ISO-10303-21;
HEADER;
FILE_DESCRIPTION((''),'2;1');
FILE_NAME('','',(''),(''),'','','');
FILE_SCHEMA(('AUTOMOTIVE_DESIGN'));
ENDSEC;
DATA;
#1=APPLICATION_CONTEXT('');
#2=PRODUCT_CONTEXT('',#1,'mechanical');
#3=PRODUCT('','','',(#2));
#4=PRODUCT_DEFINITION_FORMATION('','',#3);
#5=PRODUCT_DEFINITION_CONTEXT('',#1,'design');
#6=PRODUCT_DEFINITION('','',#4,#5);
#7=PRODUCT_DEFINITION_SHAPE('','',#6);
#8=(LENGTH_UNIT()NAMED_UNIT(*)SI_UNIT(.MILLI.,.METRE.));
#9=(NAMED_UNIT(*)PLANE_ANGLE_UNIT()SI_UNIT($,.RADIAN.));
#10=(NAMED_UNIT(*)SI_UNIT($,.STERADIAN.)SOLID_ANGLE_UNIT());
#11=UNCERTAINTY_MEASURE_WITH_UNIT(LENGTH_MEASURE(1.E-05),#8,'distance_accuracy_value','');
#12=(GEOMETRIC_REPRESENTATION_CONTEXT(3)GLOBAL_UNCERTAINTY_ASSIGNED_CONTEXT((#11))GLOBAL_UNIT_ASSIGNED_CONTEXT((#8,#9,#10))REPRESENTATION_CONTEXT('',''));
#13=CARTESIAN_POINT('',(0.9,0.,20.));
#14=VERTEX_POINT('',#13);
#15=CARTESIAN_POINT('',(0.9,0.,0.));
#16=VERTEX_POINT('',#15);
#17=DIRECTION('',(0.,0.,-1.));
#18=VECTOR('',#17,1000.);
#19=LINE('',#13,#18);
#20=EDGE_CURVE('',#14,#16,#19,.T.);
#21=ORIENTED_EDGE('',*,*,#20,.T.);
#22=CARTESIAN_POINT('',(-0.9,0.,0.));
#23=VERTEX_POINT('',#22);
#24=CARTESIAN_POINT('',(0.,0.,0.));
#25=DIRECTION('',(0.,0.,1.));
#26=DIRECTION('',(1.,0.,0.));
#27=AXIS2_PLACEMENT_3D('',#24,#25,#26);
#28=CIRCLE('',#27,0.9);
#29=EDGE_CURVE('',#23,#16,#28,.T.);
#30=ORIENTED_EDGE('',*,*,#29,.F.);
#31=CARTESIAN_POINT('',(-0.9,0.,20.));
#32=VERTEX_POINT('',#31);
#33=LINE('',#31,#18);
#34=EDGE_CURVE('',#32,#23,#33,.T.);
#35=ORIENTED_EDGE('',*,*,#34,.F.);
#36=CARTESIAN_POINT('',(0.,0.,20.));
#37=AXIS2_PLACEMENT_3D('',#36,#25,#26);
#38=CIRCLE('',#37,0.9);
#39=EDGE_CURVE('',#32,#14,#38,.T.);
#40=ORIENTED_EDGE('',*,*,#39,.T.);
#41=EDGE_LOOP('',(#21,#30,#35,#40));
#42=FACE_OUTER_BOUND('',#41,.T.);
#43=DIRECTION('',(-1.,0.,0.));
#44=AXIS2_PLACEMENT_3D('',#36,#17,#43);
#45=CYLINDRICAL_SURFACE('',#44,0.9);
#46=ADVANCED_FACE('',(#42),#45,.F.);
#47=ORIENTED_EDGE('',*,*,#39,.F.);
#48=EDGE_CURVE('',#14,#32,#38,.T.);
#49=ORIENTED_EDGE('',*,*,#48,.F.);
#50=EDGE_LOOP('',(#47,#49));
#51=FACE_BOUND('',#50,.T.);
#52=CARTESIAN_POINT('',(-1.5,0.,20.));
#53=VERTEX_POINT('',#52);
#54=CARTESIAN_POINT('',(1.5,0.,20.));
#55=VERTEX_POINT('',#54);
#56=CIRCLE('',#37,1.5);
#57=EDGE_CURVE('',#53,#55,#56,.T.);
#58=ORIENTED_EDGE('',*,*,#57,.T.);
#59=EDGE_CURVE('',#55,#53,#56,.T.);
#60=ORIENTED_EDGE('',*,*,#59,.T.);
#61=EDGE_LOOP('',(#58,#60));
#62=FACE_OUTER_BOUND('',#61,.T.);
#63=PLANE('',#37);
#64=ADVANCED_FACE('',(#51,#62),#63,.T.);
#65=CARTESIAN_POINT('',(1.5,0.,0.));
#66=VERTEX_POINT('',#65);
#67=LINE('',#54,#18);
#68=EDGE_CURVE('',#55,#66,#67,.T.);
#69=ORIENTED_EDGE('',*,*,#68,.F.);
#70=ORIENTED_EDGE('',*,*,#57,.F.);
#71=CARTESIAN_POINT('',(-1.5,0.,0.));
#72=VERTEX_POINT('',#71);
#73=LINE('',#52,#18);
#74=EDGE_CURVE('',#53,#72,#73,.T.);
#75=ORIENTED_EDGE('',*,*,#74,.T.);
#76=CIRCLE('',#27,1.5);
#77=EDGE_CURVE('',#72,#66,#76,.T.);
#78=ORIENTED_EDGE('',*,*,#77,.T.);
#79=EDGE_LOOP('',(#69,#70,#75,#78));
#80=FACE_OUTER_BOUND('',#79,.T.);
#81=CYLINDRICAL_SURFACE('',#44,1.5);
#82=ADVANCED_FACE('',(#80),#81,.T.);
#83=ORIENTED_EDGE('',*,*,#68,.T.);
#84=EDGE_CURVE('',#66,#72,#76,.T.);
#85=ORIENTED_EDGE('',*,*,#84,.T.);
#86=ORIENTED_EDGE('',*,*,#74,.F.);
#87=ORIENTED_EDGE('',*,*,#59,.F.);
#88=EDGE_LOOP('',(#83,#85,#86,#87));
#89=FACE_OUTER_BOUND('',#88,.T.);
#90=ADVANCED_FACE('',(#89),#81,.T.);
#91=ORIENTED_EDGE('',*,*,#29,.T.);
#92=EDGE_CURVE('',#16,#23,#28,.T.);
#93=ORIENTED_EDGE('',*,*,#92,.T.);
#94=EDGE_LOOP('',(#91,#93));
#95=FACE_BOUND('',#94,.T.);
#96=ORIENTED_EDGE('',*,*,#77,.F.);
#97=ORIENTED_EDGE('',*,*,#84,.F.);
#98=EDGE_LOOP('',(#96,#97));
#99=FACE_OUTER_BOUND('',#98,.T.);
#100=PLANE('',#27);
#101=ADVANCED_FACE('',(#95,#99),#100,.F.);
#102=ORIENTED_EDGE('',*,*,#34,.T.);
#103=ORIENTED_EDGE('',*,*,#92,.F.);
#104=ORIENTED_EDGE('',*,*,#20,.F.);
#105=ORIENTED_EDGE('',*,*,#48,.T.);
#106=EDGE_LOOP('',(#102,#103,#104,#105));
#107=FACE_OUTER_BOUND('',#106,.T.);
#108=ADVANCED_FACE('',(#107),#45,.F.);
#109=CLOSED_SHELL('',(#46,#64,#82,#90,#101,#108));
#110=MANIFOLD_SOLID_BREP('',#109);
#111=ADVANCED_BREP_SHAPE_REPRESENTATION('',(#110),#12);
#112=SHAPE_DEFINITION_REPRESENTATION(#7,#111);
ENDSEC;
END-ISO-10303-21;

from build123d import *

# Parameters (mm, degrees)
SKETCH_1_R      = 1.5
SKETCH_1_R_2    = 0.9
EXTRUDE_1_DEPTH = 20


with BuildPart() as part:
    # 草图1 → 拉伸1 (new body)
    with BuildSketch(Plane.XY):
        Circle(SKETCH_1_R)
        Circle(SKETCH_1_R_2, mode=Mode.SUBTRACT)
    extrude(amount=EXTRUDE_1_DEPTH)


solid = part.part
